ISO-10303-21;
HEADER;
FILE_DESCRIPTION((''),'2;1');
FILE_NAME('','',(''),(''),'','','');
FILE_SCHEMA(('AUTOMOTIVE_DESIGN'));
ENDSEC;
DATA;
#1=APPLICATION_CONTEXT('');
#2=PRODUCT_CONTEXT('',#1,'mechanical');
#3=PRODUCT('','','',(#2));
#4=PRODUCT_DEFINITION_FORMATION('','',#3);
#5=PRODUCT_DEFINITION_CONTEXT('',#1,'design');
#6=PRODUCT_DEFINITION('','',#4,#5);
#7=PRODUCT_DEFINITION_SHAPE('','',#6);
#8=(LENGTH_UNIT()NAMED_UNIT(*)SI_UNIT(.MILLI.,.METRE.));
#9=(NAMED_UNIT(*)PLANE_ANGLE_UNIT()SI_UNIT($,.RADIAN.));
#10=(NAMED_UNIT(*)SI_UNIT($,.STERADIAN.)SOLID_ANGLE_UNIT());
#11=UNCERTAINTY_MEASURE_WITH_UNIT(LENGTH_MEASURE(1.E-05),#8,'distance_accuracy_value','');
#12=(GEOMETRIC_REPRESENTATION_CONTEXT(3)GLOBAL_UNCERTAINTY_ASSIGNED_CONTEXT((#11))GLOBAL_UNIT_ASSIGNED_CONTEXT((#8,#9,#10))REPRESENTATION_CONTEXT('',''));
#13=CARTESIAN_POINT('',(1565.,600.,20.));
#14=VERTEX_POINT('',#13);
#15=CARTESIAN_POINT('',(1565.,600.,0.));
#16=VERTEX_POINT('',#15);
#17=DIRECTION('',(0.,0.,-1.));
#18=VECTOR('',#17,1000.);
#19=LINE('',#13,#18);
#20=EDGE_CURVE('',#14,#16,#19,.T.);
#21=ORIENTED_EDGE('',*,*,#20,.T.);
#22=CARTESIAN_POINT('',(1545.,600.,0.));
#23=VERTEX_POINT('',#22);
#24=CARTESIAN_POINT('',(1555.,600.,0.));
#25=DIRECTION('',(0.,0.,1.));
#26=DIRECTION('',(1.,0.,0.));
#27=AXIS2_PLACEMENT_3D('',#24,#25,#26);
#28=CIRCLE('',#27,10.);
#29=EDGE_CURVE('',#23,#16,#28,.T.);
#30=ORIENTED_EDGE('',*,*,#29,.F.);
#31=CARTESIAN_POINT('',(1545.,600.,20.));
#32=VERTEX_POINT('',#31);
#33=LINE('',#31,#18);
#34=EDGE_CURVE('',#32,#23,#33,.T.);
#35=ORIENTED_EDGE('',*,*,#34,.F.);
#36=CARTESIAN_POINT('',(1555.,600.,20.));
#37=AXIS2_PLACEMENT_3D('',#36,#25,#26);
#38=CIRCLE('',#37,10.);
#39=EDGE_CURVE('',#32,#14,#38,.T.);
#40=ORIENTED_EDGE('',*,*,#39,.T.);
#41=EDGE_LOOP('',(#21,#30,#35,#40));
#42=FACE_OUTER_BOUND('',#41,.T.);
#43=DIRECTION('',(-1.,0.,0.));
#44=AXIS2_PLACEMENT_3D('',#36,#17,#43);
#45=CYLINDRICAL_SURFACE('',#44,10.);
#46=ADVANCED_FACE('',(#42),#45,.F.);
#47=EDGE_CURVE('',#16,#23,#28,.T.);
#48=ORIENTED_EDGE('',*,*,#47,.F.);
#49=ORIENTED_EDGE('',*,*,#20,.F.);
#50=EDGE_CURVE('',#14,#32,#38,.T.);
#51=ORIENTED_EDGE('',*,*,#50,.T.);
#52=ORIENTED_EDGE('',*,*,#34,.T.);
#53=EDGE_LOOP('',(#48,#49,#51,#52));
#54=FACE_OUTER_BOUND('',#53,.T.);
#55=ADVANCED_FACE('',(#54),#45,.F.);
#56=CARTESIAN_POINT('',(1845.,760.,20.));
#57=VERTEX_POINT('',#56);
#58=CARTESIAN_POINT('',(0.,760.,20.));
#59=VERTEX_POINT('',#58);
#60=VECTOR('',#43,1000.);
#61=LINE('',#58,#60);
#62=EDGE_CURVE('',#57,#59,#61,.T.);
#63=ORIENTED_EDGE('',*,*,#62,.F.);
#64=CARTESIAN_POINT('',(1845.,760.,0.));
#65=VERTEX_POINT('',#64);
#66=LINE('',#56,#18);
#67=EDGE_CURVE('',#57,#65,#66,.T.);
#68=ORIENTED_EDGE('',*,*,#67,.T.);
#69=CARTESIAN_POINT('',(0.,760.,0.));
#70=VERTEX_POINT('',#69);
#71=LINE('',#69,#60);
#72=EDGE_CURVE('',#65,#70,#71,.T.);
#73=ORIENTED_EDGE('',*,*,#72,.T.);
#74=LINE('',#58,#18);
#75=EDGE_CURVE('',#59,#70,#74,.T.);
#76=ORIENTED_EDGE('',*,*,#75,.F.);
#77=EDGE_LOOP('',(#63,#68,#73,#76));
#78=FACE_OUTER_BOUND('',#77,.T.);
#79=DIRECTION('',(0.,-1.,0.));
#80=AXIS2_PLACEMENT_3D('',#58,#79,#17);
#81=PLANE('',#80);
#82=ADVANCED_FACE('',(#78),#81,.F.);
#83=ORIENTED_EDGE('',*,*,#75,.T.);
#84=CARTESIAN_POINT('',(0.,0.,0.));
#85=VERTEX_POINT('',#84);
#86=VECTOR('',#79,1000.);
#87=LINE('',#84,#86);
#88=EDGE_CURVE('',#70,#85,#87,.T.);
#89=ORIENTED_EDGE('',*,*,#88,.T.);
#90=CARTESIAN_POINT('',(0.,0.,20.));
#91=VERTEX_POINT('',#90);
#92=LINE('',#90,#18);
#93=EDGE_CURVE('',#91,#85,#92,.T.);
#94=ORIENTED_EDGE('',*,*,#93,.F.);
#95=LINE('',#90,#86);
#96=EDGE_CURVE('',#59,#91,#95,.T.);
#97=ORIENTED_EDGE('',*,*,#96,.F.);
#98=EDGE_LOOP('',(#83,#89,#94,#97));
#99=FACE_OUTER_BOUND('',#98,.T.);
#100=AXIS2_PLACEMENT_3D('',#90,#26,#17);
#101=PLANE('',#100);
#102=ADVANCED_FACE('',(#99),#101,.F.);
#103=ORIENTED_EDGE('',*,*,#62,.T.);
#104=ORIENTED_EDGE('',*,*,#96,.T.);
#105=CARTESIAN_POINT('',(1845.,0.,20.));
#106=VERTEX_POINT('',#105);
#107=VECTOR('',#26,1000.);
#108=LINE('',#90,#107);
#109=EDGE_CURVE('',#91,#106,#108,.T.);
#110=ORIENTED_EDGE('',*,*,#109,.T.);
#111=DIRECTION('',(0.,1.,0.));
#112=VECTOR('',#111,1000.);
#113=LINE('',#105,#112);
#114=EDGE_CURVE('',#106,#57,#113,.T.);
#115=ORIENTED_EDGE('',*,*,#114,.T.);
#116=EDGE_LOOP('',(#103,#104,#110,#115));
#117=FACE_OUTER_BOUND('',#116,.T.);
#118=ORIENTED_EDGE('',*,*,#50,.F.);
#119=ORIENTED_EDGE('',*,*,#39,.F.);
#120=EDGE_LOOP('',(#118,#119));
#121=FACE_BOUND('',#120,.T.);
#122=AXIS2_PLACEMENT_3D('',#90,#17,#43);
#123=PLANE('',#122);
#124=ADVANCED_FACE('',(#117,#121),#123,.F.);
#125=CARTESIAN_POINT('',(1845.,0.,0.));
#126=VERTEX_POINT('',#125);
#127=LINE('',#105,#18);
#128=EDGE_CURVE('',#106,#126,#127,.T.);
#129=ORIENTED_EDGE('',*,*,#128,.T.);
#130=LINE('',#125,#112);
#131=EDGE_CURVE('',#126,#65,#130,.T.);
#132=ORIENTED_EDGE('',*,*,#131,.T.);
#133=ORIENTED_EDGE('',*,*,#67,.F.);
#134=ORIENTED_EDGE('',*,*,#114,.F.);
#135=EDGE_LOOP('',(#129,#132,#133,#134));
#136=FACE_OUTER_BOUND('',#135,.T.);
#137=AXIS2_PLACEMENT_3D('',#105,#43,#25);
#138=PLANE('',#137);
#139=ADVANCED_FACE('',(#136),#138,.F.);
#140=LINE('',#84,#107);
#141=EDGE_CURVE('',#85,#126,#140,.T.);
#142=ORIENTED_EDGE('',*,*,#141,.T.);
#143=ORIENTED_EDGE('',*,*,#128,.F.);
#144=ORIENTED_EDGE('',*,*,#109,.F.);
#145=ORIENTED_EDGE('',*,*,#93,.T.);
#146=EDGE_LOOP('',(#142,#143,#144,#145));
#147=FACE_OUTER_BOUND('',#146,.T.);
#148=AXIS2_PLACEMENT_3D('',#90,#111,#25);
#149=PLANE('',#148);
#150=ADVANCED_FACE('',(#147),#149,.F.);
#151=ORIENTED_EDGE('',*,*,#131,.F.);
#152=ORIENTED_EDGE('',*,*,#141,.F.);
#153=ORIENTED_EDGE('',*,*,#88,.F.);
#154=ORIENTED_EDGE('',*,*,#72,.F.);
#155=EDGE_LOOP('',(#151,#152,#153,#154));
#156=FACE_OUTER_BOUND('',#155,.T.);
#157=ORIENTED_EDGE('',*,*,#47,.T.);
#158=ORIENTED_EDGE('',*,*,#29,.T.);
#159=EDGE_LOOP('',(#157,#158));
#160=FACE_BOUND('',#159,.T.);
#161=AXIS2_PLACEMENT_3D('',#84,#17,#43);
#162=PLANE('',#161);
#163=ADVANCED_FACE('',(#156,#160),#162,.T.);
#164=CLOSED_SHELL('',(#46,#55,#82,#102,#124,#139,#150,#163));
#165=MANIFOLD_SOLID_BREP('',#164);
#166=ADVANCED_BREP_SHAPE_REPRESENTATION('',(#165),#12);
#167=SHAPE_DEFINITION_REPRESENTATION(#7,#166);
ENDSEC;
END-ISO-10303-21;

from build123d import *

# Parameters (mm, degrees)
SKETCH1_W           = 1845
SKETCH1_H           = 760
SKETCH1_R           = 10
BOSS_EXTRUDE1_DEPTH = 20


with BuildPart() as part:
    # Sketch1 → Boss-Extrude1 (new body)
    with BuildSketch(Plane.XY):
        with Locations((922.5, 380)):
            Rectangle(SKETCH1_W, SKETCH1_H)
        with Locations((1555, 600)):
            Circle(SKETCH1_R, mode=Mode.SUBTRACT)
    extrude(amount=BOSS_EXTRUDE1_DEPTH)


solid = part.part
